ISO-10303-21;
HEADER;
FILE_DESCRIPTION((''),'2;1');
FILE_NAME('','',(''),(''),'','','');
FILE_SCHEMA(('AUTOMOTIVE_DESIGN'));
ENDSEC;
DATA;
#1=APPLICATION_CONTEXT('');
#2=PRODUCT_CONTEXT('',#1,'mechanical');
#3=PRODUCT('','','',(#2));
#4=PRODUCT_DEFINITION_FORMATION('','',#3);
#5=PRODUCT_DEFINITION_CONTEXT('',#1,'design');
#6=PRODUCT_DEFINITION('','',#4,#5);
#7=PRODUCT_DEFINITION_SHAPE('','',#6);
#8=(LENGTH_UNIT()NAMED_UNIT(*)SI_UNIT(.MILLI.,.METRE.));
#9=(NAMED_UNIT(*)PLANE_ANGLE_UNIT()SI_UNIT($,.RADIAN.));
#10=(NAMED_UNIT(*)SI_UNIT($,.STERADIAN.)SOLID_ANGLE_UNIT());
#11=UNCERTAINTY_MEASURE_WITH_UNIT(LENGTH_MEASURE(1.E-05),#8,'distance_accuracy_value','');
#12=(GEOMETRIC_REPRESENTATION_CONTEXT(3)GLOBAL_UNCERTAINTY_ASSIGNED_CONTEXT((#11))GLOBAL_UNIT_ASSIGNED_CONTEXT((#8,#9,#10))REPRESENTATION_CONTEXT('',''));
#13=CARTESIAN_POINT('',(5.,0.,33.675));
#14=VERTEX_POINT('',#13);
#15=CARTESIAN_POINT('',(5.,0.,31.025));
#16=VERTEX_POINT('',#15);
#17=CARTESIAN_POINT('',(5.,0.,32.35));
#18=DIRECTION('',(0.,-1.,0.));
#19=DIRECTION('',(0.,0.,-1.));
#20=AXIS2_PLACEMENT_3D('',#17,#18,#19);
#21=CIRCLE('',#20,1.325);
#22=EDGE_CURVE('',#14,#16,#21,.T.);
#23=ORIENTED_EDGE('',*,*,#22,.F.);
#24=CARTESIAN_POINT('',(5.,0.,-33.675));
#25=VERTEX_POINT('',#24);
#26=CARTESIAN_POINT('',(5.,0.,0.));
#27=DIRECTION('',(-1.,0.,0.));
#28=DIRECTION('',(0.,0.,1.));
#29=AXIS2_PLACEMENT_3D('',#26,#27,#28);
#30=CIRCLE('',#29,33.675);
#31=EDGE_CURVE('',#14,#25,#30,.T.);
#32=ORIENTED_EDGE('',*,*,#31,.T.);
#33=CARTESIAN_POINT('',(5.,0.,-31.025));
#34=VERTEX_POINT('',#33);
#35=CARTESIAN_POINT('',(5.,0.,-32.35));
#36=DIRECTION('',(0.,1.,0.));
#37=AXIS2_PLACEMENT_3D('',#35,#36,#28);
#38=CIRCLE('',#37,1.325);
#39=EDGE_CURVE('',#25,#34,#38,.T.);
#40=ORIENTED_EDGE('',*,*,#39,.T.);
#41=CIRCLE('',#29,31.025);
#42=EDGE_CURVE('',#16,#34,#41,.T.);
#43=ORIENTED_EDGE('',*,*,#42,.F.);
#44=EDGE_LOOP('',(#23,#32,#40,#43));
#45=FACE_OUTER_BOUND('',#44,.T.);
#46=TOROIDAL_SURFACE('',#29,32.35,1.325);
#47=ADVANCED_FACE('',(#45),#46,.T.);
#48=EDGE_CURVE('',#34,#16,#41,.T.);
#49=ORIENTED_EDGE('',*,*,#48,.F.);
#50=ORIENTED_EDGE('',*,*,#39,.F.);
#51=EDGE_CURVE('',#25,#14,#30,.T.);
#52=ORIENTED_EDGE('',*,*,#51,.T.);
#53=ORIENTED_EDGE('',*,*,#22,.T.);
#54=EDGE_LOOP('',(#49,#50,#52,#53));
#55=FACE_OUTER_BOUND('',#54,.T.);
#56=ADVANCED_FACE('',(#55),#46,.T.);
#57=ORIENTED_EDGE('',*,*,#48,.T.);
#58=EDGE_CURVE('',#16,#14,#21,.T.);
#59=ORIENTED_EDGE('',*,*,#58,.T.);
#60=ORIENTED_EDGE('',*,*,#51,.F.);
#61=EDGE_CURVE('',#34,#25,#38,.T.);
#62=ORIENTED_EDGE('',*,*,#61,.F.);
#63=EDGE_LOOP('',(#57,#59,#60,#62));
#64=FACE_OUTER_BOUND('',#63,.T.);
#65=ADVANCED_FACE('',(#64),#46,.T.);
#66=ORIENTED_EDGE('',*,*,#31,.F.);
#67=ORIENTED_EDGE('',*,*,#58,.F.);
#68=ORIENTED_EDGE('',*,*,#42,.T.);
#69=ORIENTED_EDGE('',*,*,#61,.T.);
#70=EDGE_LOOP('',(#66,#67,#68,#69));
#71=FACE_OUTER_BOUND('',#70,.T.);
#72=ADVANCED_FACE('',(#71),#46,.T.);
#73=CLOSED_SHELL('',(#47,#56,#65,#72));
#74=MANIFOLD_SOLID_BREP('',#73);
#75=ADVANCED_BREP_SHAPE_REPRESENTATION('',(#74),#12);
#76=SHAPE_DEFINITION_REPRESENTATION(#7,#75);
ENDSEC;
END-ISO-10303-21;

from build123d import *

# Parameters (mm, degrees)
SKETCH1_R = 1.325


with BuildPart() as part:
    # Sketch1 → Revolve1 (revolve)
    with BuildSketch(Plane.XY, mode=Mode.PRIVATE) as revolve1_sk:
        with Locations((5, 32.35)):
            Circle(SKETCH1_R)
    revolve(revolve1_sk.sketch.rotate(Axis((0, 0, 0), (1, 0, 0)), 90), axis=Axis((0, 0, 0), (1, 0, 0)))


solid = part.part
